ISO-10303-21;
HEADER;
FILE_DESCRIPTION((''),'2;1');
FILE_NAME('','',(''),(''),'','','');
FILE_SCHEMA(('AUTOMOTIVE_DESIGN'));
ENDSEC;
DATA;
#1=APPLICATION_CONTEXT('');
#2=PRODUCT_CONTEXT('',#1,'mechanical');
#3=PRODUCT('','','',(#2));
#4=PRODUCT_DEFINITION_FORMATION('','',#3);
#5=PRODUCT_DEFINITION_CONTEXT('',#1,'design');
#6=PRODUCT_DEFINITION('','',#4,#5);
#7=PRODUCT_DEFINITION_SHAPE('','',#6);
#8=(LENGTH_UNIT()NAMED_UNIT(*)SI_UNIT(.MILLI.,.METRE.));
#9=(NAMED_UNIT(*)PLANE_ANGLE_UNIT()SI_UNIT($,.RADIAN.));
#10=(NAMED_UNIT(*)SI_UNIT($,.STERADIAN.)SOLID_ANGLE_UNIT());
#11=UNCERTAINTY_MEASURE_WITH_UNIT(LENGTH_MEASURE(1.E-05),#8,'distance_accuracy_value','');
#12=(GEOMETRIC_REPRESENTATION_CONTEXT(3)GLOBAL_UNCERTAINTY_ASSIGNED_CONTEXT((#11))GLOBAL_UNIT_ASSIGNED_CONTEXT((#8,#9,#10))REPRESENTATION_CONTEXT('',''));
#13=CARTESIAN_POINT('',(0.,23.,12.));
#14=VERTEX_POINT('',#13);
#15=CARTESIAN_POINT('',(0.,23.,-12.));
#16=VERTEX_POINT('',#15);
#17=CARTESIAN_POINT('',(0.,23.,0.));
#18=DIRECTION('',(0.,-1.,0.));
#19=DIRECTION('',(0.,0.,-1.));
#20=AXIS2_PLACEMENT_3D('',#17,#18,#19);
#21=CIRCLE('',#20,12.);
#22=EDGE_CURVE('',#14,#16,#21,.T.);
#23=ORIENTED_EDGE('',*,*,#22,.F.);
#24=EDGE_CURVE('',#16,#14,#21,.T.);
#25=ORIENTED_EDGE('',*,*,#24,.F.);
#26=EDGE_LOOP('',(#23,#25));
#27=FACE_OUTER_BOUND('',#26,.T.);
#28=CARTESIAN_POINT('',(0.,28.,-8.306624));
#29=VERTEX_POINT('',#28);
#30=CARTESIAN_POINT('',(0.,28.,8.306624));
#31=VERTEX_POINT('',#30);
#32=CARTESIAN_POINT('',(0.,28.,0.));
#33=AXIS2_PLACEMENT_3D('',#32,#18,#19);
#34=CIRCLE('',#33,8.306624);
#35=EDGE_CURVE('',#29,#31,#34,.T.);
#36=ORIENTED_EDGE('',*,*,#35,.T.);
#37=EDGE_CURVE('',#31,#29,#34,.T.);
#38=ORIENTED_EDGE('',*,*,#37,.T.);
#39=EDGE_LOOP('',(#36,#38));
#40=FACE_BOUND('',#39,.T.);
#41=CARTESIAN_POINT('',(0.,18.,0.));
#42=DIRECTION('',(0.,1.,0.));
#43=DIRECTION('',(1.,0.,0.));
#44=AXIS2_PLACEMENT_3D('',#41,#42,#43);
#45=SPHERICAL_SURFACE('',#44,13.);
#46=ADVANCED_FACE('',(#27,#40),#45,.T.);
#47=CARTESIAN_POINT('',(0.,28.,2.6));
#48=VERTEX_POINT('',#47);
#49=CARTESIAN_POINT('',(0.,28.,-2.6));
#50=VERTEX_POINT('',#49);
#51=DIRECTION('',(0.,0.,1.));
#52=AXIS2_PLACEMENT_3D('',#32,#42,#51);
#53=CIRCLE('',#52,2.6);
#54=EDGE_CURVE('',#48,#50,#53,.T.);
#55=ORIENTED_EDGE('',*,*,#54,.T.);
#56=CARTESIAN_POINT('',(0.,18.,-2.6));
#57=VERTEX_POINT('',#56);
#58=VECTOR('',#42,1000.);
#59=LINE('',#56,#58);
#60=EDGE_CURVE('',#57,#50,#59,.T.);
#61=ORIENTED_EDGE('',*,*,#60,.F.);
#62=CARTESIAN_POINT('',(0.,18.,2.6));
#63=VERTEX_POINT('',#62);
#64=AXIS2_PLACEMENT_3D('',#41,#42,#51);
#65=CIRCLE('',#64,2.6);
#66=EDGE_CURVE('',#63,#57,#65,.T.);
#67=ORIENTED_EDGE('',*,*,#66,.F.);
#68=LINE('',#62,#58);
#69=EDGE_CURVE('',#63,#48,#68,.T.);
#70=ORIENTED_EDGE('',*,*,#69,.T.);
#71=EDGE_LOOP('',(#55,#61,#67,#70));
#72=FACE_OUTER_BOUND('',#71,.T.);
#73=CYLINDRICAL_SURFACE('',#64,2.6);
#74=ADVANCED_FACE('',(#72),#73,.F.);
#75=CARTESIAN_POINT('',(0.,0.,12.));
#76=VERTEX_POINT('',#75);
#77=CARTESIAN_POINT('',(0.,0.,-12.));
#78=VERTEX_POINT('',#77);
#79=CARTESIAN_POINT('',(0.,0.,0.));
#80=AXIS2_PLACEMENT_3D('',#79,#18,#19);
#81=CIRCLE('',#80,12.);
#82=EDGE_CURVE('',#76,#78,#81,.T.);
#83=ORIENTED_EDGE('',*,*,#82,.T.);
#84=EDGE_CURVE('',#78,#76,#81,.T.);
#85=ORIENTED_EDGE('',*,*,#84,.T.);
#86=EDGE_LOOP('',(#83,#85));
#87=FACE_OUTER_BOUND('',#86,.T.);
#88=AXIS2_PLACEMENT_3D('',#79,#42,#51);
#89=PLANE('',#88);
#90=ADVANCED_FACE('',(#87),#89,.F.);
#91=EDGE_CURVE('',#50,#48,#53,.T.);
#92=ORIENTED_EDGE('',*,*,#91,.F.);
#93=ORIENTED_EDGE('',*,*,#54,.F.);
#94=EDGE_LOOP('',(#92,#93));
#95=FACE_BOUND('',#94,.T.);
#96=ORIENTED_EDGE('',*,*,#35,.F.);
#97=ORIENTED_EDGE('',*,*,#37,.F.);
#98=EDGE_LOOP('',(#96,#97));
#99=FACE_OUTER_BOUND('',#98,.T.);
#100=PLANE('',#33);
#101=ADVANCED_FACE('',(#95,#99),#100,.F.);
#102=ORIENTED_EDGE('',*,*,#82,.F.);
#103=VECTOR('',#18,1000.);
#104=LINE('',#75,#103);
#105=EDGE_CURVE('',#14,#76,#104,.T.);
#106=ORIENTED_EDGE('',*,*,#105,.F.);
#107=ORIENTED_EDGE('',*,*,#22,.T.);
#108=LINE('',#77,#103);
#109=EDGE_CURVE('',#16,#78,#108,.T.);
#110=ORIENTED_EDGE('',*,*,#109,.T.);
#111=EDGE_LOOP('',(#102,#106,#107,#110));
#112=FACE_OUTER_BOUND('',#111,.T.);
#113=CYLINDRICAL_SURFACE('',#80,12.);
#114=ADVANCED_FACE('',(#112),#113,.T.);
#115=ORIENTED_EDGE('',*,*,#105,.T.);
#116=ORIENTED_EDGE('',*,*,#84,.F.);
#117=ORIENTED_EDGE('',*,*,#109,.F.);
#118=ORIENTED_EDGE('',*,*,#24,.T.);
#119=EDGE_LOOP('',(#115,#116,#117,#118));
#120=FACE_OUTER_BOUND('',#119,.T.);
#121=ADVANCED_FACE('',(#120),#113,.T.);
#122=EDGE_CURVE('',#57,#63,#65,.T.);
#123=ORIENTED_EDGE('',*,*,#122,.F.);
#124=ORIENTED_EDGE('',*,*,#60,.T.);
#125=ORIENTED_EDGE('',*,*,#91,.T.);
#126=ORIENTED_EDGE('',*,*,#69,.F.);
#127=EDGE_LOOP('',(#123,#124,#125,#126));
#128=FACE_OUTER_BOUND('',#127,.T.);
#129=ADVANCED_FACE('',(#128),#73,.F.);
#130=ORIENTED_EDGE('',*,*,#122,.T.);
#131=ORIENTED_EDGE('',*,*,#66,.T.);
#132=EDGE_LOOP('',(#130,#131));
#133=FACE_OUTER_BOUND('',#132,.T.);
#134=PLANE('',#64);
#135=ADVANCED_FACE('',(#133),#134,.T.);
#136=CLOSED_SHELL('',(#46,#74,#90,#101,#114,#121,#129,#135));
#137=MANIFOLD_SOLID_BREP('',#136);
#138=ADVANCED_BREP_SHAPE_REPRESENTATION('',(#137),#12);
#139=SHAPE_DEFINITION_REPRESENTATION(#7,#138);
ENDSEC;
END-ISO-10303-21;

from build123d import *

# Parameters (mm, degrees)
CAP_BODY_PROFILE_SKETCH_W = 12
CAP_BODY_PROFILE_SKETCH_H = 23
TOP_DOME_8MM_FACE_RADIUS  = 12
TOP_DOME_8MM_HEIGHT       = 8
CENTRE_HOLE_SKETCH_R      = 2.6
CENTRE_HOLE_5_2X10_DEPTH  = 10


with BuildPart() as part:
    # Cap Body Profile Sketch → Cap Body _24x23 (revolve)
    with BuildSketch(Plane(origin=(0, 0, 0), x_dir=(0, 0, -1), z_dir=(1, 0, 0)), mode=Mode.PRIVATE) as cap_body_24x23_sk:
        with Locations((-6, 11.5)):
            Rectangle(CAP_BODY_PROFILE_SKETCH_W, CAP_BODY_PROFILE_SKETCH_H)
    revolve(cap_body_24x23_sk.sketch.rotate(Axis((0, 0, 0), (0, 1, 0)), 180), axis=Axis((0, 0, 0), (0, 1, 0)))

    # Top Dome 8mm: a dome of height H over a round flat face of radius A is a cap of a sphere of radius (A * A + H * H) / (2 * H)
    top_dome_8mm_r = (TOP_DOME_8MM_FACE_RADIUS * TOP_DOME_8MM_FACE_RADIUS + TOP_DOME_8MM_HEIGHT * TOP_DOME_8MM_HEIGHT) / (2 * TOP_DOME_8MM_HEIGHT)
    top_dome_8mm_base = Plane((0, 23, 0), z_dir=(0, 1, 0))
    with Locations(top_dome_8mm_base.offset(TOP_DOME_8MM_HEIGHT - top_dome_8mm_r)):
        top_dome_8mm_ball = Sphere(top_dome_8mm_r, mode=Mode.PRIVATE)
    add(split(top_dome_8mm_ball, bisect_by=top_dome_8mm_base, keep=Keep.TOP, mode=Mode.PRIVATE))

    # Dome Top Flat Trim
    split(bisect_by=Plane(origin=(0, 28, 0), x_dir=(-1, 0, 0), z_dir=(0, -1, 0)), keep=Keep.TOP)

    # Centre Hole Sketch → Centre Hole _5.2x10 (cut)
    with BuildSketch(Plane(origin=(0, 28, 0), x_dir=(1, 0, 0), z_dir=(0, 1, 0))):
        with Locations(Location((0, 0, 0), (0, 0, 270))):
            Circle(CENTRE_HOLE_SKETCH_R)
    extrude(amount=-CENTRE_HOLE_5_2X10_DEPTH, mode=Mode.SUBTRACT)


solid = part.part
